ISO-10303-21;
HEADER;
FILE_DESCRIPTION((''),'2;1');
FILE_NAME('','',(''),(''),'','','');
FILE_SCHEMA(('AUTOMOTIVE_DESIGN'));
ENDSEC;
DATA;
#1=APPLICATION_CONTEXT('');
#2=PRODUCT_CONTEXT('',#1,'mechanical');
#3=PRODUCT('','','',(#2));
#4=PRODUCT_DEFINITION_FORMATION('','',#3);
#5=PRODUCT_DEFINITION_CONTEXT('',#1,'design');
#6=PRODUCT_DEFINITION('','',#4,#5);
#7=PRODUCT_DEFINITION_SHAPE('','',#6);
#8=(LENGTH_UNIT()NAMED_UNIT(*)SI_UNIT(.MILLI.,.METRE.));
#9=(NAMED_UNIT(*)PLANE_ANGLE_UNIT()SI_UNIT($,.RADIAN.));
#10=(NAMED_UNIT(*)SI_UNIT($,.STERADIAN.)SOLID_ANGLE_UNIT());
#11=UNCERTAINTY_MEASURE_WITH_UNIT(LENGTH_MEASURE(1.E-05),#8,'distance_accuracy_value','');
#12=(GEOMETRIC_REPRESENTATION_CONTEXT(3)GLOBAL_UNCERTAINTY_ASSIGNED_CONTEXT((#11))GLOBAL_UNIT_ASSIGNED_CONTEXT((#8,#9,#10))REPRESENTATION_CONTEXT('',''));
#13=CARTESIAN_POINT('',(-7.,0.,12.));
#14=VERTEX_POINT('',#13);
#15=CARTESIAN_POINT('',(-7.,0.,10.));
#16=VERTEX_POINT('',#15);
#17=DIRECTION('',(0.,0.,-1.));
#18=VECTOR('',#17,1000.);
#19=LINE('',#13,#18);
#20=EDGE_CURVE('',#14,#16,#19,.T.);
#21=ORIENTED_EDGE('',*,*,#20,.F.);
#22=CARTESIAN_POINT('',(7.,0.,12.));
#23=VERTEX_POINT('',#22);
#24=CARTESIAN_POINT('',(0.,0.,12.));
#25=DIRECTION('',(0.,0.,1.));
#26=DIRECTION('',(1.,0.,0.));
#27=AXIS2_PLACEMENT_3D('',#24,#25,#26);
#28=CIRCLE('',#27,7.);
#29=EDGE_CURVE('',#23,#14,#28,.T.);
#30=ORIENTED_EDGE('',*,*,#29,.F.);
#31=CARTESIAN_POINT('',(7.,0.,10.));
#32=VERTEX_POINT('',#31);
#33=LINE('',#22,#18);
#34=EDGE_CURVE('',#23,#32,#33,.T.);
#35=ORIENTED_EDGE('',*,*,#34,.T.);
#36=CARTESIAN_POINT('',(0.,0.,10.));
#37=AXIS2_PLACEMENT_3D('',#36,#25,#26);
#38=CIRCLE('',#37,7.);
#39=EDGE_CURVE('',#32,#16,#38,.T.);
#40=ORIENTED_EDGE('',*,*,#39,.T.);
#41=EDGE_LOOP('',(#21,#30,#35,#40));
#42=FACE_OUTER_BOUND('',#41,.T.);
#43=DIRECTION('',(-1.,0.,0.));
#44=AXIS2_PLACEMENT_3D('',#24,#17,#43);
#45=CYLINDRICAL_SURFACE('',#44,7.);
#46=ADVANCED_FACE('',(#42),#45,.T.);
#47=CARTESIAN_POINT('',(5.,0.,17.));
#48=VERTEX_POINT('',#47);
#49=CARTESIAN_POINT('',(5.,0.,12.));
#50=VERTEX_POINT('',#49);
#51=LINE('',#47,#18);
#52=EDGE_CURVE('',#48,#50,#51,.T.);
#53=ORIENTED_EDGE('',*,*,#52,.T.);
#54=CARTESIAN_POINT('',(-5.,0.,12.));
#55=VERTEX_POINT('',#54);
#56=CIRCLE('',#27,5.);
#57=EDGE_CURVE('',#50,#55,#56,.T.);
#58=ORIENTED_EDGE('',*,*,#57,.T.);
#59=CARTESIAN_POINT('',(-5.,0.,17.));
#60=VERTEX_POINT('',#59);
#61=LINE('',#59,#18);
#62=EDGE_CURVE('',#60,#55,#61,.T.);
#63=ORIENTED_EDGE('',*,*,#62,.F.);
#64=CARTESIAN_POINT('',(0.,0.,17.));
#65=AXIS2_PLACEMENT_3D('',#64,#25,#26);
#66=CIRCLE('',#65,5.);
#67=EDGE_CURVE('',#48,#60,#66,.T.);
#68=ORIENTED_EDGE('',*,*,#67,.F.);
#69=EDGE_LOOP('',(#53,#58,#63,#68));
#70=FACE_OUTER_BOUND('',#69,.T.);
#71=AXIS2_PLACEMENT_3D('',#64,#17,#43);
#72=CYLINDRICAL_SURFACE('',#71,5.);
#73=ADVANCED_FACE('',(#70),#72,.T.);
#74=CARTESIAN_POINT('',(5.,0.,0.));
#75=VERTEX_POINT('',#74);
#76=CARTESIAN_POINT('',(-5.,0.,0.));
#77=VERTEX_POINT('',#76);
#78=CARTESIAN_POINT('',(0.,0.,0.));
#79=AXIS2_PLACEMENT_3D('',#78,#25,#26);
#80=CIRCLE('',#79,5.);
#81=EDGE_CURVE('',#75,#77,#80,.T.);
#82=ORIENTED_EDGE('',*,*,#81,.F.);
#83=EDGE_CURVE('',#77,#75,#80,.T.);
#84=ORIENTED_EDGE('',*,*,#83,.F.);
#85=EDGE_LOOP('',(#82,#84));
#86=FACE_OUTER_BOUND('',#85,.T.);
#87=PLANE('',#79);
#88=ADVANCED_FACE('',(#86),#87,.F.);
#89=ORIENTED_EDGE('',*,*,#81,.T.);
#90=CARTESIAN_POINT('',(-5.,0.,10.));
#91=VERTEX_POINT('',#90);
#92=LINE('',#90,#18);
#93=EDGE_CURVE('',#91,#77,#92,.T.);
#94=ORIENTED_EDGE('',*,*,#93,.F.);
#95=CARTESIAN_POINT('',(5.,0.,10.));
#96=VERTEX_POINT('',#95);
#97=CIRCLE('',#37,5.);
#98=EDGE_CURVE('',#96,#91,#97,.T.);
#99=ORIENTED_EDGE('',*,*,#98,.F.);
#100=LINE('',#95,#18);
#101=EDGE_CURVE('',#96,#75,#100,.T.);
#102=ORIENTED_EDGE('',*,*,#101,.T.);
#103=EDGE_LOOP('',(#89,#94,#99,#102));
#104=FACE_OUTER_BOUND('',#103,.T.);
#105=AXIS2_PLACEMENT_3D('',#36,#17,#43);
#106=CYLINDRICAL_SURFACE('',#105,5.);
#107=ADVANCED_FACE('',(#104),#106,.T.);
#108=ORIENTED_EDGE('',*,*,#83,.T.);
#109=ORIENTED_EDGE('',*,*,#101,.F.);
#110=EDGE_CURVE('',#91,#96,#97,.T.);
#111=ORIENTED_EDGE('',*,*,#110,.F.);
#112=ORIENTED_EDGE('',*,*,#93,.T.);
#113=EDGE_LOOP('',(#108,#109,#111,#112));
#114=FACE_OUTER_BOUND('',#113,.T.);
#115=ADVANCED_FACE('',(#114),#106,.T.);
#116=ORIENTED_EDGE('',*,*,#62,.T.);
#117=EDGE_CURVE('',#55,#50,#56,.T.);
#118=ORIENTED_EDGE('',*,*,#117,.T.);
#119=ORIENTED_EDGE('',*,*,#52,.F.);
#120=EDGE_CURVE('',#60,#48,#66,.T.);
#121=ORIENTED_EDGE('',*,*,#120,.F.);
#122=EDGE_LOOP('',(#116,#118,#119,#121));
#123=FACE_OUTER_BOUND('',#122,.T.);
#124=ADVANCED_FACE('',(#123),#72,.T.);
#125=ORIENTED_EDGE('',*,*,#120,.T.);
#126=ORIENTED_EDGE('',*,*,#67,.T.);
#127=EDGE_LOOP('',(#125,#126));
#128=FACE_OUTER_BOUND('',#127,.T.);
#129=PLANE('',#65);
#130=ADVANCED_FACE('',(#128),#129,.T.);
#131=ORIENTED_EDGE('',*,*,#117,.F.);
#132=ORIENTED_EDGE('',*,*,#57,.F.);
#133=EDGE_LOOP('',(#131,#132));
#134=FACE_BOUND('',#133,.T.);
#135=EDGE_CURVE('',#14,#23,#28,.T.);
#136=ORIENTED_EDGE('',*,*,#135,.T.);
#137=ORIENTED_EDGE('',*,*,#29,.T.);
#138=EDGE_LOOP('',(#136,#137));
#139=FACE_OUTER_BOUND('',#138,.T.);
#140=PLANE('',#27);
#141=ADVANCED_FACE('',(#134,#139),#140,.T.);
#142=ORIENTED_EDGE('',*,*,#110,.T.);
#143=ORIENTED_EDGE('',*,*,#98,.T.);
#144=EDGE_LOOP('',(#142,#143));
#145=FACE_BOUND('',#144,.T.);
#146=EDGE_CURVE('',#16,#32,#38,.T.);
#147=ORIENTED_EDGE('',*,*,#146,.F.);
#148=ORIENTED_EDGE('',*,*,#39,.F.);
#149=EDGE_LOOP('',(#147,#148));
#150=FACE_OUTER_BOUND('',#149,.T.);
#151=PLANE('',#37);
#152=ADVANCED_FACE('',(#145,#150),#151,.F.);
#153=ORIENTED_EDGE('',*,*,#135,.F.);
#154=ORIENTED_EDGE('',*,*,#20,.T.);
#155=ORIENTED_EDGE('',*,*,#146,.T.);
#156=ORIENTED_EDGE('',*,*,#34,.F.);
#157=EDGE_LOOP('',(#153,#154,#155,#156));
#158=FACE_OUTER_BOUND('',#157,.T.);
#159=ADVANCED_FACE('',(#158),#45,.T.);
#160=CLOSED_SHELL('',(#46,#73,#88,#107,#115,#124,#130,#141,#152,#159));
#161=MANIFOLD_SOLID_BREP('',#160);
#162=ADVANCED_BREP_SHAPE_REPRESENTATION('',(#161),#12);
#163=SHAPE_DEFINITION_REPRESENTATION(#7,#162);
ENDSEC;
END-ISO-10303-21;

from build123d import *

# Parameters (mm, degrees)
SKETCH1_R           = 5
BOSS_EXTRUDE1_DEPTH = 10
SKETCH2_R           = 7
BOSS_EXTRUDE2_DEPTH = 2
SKETCH4_R           = 5
BOSS_EXTRUDE3_DEPTH = 5


with BuildPart() as part:
    # Sketch1 → Boss-Extrude1 (new body)
    with BuildSketch(Plane.XY):
        Circle(SKETCH1_R)
    extrude(amount=BOSS_EXTRUDE1_DEPTH)

    # Sketch2 → Boss-Extrude2 (add)
    with BuildSketch(Plane.XY.offset(10)):
        Circle(SKETCH2_R)
    extrude(amount=BOSS_EXTRUDE2_DEPTH)

    # Sketch4 → Boss-Extrude3 (add)
    with BuildSketch(Plane.XY.offset(12)):
        Circle(SKETCH4_R)
    extrude(amount=BOSS_EXTRUDE3_DEPTH)


solid = part.part
